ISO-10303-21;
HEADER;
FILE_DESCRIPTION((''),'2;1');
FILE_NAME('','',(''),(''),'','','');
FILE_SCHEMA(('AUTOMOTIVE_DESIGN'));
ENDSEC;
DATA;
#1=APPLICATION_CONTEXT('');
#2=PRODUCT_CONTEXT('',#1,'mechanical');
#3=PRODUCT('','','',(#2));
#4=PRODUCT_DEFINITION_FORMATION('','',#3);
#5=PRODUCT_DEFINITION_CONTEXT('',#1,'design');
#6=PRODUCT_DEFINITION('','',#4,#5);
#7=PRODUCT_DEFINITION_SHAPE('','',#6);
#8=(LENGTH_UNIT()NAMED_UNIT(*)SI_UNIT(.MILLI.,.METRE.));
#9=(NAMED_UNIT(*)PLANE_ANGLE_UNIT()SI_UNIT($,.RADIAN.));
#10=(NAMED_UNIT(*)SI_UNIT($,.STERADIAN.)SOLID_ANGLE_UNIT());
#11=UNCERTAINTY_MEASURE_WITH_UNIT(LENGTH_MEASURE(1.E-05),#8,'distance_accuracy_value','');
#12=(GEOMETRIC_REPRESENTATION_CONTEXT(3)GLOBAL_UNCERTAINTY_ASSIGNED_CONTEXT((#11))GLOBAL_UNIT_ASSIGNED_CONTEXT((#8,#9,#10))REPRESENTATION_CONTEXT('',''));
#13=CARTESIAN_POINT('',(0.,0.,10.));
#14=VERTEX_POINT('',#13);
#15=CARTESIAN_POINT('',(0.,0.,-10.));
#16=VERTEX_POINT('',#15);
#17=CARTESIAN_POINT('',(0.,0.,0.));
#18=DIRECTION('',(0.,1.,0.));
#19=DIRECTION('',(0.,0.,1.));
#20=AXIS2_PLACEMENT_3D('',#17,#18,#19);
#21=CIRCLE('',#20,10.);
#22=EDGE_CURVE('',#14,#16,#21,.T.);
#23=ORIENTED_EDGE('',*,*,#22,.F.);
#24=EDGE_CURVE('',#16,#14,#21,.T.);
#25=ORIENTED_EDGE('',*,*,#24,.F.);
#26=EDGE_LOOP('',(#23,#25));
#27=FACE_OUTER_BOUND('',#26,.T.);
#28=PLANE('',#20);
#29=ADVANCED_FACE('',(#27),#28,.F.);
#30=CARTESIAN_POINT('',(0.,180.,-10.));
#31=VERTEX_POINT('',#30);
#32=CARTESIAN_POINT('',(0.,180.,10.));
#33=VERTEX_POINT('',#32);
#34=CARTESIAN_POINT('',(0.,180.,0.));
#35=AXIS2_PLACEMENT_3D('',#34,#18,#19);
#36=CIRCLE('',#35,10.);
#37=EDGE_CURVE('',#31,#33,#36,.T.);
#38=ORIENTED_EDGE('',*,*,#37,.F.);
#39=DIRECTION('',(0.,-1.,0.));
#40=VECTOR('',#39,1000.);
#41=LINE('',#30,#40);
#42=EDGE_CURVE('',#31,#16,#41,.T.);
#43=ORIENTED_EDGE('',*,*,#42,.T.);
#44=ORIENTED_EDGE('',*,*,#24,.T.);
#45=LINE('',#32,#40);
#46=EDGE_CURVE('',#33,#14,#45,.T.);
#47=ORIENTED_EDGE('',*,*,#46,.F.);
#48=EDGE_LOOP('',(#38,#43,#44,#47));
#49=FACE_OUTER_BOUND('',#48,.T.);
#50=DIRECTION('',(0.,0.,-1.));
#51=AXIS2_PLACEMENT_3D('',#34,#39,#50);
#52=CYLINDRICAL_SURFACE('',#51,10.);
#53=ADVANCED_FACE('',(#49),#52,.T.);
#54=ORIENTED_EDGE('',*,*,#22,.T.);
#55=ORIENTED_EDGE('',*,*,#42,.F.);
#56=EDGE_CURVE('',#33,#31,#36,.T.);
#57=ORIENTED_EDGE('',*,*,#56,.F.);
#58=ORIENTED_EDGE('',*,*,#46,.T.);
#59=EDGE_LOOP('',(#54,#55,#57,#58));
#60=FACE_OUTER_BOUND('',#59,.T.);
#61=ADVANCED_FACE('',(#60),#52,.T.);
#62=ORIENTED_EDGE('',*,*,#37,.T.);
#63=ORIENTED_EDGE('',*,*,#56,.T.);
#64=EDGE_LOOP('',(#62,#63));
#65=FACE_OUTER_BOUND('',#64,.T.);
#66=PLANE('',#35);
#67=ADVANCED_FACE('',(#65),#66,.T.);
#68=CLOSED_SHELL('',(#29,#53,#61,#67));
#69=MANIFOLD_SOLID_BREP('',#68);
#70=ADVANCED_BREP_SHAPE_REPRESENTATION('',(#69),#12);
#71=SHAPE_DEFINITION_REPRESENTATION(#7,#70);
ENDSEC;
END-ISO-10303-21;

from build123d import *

# Parameters (mm, degrees)
SKETCH1_R           = 10
BOSS_EXTRUDE1_DEPTH = 180


with BuildPart() as part:
    # Sketch1 → Boss-Extrude1 (new body)
    with BuildSketch(Plane(origin=(0, 0, 0), x_dir=(1, 0, 0), z_dir=(0, 1, 0))):
        with Locations(Location((0, 0, 0), (0, 0, 90))):
            Circle(SKETCH1_R)
    extrude(amount=BOSS_EXTRUDE1_DEPTH)


solid = part.part
